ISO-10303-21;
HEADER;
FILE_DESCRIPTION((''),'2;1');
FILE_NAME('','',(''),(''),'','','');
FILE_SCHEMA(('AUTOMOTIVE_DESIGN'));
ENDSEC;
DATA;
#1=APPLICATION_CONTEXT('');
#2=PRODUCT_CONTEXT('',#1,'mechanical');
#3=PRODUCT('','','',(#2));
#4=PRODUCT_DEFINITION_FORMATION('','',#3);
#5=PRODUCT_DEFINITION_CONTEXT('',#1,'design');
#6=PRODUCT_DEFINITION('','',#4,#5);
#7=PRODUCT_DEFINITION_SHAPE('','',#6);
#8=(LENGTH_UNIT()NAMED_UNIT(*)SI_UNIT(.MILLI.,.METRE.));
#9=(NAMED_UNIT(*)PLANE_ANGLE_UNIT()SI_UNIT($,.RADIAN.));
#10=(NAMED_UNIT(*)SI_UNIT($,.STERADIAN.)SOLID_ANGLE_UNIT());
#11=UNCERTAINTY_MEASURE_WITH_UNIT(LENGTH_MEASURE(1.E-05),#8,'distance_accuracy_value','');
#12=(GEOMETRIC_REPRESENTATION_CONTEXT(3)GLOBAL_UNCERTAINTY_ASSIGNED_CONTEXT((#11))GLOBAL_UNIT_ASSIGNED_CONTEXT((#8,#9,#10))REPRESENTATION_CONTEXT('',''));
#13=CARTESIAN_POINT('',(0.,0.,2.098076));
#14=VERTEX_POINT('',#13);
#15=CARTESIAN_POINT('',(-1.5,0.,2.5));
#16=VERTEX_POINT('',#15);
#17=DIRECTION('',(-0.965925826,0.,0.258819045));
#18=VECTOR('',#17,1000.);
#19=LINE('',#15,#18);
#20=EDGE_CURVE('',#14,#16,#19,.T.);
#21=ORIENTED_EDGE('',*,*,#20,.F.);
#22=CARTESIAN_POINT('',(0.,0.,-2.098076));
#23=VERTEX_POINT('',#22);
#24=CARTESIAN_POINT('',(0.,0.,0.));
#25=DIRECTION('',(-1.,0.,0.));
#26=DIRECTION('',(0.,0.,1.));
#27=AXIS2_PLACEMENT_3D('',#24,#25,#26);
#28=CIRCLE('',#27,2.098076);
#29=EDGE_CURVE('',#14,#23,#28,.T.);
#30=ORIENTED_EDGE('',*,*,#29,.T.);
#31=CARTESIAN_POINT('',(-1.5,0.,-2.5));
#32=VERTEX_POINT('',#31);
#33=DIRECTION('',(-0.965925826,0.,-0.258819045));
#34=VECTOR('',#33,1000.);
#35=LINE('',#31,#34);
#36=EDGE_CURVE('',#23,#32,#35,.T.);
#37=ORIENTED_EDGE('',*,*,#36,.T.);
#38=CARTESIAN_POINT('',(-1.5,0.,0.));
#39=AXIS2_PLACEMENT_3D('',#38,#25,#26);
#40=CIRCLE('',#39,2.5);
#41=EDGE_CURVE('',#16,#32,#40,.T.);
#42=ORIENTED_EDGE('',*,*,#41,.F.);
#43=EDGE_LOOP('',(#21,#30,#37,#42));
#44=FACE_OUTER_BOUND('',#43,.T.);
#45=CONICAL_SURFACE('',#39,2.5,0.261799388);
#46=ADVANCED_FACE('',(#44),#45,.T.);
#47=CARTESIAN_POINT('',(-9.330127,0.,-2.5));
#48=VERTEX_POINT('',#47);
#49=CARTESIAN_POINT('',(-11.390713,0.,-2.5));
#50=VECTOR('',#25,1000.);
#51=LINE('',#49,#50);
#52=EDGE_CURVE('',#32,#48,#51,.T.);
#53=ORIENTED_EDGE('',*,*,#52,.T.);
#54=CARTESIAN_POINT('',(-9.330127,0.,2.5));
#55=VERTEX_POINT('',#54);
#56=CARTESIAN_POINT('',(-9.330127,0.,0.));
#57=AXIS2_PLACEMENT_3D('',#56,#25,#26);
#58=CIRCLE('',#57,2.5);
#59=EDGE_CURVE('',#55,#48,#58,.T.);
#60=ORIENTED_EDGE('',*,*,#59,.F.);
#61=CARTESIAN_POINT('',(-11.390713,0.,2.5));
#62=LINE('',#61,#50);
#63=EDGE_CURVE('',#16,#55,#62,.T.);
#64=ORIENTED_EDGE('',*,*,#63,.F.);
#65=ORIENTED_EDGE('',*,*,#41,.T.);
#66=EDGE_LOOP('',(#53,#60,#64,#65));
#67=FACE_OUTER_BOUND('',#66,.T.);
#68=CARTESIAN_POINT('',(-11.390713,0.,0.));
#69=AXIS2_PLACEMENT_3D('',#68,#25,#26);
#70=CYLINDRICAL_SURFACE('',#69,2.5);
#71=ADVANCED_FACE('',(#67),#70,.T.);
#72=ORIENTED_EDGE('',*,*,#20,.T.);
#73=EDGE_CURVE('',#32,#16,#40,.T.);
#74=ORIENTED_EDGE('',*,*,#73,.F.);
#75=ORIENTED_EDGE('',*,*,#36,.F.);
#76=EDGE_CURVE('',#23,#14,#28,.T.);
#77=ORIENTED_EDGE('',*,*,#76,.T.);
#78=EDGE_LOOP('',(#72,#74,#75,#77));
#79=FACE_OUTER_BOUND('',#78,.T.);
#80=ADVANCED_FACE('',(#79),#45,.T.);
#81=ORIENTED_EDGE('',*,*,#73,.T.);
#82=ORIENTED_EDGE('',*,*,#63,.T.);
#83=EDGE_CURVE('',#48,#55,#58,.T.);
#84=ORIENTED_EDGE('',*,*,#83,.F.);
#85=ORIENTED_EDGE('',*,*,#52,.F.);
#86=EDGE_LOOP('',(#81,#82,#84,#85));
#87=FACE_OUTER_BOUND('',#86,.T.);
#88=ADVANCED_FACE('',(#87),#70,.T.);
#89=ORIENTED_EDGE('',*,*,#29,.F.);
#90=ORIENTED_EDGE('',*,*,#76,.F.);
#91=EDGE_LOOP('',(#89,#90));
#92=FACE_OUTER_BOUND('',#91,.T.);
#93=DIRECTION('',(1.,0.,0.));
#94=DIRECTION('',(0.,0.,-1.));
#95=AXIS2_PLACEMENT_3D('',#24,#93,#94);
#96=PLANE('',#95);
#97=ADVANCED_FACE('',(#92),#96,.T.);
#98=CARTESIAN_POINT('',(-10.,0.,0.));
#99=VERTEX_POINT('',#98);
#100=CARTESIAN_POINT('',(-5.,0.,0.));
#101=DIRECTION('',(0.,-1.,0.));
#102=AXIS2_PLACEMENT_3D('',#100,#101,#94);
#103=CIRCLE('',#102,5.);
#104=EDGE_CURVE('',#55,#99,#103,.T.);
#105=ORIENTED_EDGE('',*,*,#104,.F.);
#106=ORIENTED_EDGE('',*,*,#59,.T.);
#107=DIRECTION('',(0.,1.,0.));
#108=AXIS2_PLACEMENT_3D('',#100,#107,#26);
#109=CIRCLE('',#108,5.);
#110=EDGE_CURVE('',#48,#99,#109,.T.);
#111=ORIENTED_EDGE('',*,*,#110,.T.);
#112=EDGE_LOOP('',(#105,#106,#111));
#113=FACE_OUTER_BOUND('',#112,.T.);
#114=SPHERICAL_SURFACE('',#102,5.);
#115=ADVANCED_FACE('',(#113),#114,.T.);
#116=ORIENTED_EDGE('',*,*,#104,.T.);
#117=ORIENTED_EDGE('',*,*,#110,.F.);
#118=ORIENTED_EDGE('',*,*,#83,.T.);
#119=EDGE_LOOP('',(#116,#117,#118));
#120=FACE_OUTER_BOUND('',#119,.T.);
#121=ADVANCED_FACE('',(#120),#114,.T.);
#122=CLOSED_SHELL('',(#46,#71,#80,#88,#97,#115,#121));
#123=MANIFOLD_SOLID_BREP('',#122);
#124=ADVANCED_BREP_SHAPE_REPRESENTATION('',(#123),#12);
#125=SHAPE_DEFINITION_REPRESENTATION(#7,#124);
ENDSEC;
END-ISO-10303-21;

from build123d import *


with BuildPart() as part:
    # Sketch1 → Revolve1 (revolve)
    with BuildSketch(Plane(origin=(0, 0, 0), x_dir=(1, 0, 0), z_dir=(0, 1, 0))):
        with BuildLine():
            Line((-1.5, -2.5), (0, -2.098076211))
            Line((0, -2.098076211), (0, 0))
            Line((0, 0), (-10, 0))
            ThreePointArc((-10, 0), (-9.829629131, -1.294095226), (-9.330127019, -2.5))
            Line((-9.330127019, -2.5), (-1.5, -2.5))
        make_face()
    revolve(axis=Axis((-11.390713055, 0, 0), (1, 0, 0)))


solid = part.part
